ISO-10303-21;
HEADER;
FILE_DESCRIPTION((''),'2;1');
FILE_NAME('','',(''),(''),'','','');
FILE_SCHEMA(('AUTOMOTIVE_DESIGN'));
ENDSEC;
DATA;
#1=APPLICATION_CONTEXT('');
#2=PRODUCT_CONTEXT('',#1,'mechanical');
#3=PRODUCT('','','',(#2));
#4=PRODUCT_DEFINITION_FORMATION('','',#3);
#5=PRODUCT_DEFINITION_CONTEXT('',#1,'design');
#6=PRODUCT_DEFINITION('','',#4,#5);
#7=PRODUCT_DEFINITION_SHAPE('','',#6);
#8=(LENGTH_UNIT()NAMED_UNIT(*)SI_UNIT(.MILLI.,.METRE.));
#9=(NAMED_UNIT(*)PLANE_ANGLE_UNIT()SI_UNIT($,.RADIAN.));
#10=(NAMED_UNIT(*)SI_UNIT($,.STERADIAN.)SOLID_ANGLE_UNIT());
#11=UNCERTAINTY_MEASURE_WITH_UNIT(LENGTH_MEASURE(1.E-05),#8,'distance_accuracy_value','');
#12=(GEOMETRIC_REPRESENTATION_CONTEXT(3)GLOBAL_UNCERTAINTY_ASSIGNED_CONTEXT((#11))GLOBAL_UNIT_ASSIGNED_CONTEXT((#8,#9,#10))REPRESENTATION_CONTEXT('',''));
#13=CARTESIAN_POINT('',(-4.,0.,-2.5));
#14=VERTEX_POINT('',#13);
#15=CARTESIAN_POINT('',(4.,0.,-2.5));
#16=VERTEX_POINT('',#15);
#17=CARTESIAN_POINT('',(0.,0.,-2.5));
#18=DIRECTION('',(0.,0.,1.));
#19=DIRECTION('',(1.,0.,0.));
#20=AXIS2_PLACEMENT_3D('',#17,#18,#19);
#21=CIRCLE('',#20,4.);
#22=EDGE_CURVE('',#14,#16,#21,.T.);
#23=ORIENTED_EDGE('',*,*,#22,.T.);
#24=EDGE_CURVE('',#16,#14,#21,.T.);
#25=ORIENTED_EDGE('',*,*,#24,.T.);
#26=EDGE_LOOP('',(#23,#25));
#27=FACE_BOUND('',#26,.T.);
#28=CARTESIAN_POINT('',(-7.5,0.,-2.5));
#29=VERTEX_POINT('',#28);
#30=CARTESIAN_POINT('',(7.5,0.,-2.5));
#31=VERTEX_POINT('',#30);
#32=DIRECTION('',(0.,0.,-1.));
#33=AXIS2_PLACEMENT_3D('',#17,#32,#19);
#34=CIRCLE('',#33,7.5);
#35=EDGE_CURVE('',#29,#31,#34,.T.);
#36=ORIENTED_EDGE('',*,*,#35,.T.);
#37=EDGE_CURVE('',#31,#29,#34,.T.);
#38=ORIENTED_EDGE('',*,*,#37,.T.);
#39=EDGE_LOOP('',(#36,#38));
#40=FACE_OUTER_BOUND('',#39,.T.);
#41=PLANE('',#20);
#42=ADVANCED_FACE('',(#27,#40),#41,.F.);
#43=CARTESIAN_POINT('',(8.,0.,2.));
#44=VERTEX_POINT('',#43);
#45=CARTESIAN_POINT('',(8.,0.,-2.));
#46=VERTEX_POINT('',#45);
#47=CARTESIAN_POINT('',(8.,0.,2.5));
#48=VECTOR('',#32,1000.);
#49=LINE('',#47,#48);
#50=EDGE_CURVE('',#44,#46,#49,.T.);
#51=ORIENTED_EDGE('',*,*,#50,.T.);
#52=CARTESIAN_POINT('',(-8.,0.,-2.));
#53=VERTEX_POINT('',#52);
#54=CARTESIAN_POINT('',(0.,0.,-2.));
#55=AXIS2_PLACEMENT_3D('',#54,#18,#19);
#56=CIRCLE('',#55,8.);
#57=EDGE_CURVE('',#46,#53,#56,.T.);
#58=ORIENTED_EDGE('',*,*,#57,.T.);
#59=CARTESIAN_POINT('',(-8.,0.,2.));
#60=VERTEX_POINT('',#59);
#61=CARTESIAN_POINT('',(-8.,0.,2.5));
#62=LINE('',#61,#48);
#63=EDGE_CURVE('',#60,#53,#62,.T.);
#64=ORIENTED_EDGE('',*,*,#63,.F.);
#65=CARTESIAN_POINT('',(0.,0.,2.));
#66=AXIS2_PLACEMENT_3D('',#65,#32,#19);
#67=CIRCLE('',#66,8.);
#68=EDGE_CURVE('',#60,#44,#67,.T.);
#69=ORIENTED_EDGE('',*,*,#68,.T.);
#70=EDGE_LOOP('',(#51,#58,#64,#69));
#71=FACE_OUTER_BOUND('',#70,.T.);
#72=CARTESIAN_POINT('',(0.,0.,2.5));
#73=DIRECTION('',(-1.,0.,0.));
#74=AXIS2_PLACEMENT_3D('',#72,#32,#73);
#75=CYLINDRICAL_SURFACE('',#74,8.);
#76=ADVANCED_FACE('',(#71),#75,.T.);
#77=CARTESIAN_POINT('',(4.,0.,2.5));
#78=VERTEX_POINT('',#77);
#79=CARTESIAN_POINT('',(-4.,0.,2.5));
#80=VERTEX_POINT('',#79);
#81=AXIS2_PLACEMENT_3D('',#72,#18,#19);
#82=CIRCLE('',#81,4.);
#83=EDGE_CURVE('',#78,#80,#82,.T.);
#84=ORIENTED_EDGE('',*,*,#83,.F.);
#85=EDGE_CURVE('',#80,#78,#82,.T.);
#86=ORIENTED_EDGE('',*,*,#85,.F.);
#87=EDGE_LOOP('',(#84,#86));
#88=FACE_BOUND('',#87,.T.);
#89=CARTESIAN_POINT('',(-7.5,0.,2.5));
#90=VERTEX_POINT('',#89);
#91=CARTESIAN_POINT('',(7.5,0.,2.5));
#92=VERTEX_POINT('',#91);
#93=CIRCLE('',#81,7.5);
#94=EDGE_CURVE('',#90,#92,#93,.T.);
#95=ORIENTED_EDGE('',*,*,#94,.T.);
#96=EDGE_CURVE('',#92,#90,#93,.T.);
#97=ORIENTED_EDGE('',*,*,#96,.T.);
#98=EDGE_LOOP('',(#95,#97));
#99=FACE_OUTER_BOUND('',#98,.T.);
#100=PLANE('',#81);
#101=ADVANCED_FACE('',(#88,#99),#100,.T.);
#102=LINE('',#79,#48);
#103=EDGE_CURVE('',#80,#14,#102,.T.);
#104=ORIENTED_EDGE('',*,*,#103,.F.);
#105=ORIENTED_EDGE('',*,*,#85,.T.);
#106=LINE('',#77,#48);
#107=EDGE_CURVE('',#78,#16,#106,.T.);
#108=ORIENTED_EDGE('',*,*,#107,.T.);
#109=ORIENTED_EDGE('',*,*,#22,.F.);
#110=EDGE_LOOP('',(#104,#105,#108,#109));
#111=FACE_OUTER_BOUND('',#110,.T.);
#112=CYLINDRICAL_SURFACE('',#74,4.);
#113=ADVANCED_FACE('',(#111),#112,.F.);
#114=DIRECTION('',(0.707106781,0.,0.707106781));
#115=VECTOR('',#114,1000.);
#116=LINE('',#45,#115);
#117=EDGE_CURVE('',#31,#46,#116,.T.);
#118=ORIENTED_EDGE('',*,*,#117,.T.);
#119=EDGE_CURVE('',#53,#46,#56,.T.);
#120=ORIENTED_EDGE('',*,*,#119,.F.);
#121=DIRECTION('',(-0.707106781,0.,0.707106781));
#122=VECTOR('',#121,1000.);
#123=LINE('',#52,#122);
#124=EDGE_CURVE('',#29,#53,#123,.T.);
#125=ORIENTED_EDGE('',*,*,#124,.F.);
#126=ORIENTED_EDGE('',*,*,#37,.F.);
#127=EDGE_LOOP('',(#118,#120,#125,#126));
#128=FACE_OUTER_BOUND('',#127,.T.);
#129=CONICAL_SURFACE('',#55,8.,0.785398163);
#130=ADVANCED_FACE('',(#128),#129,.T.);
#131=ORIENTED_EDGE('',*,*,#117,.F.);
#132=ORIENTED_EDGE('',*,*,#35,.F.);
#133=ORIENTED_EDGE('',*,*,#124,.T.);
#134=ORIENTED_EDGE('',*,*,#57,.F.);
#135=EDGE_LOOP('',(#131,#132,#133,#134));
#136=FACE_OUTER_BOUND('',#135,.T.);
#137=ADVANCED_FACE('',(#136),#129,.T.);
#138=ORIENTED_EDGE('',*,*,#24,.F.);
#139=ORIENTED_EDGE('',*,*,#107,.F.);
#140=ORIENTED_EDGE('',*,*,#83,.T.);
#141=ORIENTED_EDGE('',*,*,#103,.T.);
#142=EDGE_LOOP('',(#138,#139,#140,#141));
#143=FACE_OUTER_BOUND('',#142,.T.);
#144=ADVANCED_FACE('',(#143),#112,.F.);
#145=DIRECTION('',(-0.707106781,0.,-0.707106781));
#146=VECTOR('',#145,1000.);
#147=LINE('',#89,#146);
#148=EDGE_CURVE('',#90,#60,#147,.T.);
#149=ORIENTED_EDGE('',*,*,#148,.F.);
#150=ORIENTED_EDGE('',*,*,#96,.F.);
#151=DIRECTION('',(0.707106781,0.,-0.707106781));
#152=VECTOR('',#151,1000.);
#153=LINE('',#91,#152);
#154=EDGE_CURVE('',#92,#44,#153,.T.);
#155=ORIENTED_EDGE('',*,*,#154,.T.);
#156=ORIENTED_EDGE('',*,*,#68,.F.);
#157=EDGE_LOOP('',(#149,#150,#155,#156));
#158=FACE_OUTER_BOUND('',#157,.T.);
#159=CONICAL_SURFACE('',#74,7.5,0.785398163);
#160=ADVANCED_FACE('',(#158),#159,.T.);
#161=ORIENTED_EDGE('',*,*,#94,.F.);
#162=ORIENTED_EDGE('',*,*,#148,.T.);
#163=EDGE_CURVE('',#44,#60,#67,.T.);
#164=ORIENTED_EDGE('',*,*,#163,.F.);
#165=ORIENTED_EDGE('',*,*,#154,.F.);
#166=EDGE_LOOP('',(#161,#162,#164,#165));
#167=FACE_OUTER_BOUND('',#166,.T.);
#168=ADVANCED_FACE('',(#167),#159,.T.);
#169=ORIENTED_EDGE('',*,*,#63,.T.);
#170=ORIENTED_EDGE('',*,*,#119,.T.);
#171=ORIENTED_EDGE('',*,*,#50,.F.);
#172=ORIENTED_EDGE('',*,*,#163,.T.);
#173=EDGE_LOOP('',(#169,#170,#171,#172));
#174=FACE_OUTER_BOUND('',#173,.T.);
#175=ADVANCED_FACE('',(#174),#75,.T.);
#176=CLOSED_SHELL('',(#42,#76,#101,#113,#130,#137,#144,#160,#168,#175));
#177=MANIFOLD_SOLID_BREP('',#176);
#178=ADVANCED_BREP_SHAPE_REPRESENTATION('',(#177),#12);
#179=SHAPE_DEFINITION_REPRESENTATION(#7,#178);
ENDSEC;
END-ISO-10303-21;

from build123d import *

# Parameters (mm, degrees)
SKETCH_1_R      = 8
SKETCH_1_R_2    = 4
EXTRUDE_1_DEPTH = 2.5
CHAMFER_1_SIZE  = 0.5


with BuildPart() as part:
    # 草图1 → 凸台-拉伸1 (new, symmetric)
    with BuildSketch(Plane.XY):
        Circle(SKETCH_1_R)
        Circle(SKETCH_1_R_2, mode=Mode.SUBTRACT)
    extrude(amount=EXTRUDE_1_DEPTH, both=True)

    # 倒角1
    chamfer_1_edges = [part.edges().sort_by_distance(p)[0] for p in [
        (-8, 0, -2.5),
        (-8, 0, 2.5),
    ]]
    chamfer(chamfer_1_edges, length=CHAMFER_1_SIZE)


solid = part.part
